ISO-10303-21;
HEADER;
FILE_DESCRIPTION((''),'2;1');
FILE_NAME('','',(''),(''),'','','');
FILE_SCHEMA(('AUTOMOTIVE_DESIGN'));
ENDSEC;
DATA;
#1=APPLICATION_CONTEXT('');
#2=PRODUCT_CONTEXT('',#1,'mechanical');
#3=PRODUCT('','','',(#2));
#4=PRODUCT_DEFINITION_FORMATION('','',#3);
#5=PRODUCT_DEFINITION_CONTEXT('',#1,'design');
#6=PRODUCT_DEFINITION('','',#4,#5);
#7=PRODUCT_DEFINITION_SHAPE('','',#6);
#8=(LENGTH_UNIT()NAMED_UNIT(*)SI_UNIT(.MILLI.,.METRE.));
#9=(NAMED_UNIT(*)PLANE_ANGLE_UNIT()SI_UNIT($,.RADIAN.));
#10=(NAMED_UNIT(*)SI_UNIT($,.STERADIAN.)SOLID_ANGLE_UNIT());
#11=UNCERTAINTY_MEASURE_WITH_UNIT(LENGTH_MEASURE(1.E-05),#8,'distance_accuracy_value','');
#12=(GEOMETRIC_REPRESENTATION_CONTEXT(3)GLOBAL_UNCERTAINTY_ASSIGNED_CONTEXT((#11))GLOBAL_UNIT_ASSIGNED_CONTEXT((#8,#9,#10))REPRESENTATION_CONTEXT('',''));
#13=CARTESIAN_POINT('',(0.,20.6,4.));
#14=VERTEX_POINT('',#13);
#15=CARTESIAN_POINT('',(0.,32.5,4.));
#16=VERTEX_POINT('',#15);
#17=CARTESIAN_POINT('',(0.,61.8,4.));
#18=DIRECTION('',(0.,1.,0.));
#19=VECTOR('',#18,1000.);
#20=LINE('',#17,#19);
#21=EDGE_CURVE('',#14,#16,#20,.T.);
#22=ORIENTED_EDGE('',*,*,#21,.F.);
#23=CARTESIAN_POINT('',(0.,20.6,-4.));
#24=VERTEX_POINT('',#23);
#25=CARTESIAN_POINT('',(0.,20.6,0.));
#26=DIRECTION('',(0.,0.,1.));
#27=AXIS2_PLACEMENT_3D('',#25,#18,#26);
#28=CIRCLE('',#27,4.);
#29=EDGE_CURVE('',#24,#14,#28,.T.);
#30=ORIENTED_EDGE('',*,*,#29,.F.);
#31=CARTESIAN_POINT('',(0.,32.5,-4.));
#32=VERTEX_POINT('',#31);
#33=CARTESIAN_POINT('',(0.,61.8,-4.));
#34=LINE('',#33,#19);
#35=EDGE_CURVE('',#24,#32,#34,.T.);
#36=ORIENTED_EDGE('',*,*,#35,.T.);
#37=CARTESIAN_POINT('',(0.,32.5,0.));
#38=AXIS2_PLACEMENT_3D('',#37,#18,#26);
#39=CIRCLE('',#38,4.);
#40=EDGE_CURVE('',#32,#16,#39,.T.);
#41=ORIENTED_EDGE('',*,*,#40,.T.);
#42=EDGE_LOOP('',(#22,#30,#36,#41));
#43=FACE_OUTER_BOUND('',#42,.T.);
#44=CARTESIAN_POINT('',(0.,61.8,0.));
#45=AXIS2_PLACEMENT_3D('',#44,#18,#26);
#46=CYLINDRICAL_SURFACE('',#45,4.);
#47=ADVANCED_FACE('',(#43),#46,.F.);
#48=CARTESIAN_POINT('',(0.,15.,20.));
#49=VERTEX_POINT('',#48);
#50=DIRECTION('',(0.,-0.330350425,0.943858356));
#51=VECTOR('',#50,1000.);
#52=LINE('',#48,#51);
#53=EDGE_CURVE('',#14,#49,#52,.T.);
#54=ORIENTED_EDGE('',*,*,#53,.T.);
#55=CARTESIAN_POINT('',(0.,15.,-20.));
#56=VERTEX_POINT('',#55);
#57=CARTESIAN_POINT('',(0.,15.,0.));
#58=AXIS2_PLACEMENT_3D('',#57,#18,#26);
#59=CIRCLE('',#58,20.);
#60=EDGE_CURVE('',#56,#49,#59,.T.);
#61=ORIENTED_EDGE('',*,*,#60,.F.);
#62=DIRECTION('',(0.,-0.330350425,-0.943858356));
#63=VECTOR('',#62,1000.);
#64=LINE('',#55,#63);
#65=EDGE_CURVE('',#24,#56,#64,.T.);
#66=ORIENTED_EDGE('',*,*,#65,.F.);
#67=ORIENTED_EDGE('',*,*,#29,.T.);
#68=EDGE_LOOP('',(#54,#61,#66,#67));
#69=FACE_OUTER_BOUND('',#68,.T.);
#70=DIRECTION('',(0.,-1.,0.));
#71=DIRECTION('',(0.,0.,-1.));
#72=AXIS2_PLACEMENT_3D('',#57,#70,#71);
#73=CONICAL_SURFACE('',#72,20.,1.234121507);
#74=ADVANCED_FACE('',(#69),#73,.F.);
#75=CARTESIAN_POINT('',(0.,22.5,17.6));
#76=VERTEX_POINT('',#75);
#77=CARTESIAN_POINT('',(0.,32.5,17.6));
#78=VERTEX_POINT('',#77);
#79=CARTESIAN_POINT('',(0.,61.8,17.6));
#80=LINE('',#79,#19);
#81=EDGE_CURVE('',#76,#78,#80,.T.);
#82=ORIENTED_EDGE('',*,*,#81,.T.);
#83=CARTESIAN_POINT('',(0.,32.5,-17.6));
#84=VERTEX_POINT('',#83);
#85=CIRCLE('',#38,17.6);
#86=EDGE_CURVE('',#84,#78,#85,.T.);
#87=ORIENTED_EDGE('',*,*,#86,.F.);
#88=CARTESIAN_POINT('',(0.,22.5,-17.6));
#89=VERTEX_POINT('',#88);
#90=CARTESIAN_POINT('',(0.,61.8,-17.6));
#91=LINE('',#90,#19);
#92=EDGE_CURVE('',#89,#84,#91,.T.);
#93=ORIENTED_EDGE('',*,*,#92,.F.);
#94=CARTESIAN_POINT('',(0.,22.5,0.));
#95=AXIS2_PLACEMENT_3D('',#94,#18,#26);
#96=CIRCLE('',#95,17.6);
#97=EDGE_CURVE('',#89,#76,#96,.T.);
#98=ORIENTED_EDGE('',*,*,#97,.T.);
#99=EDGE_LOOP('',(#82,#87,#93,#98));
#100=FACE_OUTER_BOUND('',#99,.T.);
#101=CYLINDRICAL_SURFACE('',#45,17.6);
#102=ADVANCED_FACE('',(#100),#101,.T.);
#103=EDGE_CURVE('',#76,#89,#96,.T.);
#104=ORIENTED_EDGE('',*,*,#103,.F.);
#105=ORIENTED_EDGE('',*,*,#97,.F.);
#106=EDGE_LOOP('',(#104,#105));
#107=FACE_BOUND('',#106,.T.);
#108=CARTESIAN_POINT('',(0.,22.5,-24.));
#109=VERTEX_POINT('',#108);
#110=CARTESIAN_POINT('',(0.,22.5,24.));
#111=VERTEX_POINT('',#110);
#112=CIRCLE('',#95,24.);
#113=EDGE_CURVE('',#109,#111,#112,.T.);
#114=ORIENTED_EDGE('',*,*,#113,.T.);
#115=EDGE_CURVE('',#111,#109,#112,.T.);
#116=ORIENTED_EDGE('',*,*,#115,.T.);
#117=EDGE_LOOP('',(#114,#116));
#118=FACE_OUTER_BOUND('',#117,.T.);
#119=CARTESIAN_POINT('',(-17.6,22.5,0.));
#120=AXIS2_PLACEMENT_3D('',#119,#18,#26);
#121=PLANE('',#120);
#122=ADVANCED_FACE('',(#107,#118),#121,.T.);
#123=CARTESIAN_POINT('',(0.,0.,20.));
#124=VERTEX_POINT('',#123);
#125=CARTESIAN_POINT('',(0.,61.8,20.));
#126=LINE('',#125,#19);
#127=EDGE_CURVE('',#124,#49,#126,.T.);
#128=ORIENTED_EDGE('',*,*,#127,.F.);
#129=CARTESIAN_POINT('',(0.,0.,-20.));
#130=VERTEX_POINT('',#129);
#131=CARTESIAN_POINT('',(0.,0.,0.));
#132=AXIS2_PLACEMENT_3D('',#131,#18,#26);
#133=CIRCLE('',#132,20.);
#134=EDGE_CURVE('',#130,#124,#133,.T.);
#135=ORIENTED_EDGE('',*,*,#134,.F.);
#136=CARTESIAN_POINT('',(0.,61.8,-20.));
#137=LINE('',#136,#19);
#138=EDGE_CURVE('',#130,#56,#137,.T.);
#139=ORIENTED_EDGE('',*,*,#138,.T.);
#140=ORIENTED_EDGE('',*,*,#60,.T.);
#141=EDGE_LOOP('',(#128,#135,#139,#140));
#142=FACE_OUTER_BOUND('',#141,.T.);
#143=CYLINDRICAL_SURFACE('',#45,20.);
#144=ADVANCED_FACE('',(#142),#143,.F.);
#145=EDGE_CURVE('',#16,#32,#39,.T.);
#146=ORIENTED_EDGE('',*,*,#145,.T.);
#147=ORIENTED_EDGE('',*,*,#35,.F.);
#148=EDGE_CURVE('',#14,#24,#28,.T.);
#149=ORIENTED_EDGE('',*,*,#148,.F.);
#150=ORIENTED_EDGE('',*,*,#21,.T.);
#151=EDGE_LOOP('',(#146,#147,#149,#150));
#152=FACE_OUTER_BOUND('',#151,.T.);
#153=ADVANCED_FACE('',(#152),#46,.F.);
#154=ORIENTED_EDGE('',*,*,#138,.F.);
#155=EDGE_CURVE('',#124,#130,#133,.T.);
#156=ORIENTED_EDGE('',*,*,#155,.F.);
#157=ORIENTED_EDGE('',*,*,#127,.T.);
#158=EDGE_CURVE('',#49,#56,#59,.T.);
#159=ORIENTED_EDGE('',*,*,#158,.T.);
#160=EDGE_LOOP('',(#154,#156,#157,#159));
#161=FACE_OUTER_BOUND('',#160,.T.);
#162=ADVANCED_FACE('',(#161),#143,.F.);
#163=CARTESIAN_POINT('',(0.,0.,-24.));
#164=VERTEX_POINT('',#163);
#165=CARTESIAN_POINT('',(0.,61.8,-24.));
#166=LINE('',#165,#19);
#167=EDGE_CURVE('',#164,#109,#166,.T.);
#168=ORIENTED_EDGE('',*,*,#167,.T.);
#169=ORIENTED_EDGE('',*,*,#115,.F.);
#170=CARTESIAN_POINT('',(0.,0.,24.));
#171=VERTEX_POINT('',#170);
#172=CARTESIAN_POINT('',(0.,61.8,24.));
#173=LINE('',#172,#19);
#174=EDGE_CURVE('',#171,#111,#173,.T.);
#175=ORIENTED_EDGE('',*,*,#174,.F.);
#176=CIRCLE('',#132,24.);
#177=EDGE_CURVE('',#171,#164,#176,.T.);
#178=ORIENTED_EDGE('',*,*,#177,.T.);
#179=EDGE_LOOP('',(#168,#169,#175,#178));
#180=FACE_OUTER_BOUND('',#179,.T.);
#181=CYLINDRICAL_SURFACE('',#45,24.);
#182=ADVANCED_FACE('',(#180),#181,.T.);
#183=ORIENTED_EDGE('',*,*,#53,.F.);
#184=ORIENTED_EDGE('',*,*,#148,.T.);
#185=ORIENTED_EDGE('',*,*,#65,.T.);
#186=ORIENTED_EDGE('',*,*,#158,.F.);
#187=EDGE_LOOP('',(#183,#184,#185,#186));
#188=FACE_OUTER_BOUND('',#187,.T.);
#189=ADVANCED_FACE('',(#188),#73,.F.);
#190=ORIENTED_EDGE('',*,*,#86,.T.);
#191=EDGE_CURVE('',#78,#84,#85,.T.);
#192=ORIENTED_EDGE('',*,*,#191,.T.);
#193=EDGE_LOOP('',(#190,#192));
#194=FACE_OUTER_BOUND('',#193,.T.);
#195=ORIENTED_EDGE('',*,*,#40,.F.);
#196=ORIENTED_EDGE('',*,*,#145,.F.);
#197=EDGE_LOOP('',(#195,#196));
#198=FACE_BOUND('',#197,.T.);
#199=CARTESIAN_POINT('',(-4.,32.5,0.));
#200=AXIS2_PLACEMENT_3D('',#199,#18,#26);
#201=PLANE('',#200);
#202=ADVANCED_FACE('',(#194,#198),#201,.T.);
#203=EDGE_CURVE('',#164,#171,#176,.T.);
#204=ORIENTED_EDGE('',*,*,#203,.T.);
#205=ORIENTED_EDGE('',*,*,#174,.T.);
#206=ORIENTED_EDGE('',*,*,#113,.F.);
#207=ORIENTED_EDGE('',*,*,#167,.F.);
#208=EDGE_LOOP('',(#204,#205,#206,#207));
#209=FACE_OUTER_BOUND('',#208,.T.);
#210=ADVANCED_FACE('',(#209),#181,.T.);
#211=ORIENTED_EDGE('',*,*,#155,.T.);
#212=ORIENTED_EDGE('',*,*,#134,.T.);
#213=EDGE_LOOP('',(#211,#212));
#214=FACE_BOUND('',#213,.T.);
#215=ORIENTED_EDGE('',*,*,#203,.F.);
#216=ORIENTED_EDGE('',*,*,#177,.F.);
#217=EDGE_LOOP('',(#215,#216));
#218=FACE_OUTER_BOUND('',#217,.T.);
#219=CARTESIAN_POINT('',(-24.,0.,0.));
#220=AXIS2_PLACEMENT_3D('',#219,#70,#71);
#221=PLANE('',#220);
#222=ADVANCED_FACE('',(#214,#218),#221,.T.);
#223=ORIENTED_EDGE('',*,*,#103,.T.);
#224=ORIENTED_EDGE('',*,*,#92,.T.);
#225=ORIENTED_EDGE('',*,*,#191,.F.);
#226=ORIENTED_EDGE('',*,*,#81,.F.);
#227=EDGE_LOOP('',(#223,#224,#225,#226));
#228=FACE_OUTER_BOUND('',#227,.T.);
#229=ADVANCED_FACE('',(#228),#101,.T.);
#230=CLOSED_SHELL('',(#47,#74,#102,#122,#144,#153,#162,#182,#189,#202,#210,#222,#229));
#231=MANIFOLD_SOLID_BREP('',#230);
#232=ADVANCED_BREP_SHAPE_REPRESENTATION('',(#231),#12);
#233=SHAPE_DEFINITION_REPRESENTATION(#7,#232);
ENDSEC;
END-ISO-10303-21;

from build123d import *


with BuildPart() as part:
    # 草图1 → 旋转1 (revolve)
    with BuildSketch(Plane.XY, mode=Mode.PRIVATE) as revolve_1_sk:
        Polygon((-4, 32.5), (-17.6, 32.5), (-17.6, 22.5), (-24, 22.5), (-24, 0), (-20, 0), (-20, 15), (-4, 20.6), align=None)
    revolve(revolve_1_sk.sketch.rotate(Axis((0, 61.8, 0), (0, -1, 0)), 270), axis=Axis((0, 61.8, 0), (0, -1, 0)))


solid = part.part
